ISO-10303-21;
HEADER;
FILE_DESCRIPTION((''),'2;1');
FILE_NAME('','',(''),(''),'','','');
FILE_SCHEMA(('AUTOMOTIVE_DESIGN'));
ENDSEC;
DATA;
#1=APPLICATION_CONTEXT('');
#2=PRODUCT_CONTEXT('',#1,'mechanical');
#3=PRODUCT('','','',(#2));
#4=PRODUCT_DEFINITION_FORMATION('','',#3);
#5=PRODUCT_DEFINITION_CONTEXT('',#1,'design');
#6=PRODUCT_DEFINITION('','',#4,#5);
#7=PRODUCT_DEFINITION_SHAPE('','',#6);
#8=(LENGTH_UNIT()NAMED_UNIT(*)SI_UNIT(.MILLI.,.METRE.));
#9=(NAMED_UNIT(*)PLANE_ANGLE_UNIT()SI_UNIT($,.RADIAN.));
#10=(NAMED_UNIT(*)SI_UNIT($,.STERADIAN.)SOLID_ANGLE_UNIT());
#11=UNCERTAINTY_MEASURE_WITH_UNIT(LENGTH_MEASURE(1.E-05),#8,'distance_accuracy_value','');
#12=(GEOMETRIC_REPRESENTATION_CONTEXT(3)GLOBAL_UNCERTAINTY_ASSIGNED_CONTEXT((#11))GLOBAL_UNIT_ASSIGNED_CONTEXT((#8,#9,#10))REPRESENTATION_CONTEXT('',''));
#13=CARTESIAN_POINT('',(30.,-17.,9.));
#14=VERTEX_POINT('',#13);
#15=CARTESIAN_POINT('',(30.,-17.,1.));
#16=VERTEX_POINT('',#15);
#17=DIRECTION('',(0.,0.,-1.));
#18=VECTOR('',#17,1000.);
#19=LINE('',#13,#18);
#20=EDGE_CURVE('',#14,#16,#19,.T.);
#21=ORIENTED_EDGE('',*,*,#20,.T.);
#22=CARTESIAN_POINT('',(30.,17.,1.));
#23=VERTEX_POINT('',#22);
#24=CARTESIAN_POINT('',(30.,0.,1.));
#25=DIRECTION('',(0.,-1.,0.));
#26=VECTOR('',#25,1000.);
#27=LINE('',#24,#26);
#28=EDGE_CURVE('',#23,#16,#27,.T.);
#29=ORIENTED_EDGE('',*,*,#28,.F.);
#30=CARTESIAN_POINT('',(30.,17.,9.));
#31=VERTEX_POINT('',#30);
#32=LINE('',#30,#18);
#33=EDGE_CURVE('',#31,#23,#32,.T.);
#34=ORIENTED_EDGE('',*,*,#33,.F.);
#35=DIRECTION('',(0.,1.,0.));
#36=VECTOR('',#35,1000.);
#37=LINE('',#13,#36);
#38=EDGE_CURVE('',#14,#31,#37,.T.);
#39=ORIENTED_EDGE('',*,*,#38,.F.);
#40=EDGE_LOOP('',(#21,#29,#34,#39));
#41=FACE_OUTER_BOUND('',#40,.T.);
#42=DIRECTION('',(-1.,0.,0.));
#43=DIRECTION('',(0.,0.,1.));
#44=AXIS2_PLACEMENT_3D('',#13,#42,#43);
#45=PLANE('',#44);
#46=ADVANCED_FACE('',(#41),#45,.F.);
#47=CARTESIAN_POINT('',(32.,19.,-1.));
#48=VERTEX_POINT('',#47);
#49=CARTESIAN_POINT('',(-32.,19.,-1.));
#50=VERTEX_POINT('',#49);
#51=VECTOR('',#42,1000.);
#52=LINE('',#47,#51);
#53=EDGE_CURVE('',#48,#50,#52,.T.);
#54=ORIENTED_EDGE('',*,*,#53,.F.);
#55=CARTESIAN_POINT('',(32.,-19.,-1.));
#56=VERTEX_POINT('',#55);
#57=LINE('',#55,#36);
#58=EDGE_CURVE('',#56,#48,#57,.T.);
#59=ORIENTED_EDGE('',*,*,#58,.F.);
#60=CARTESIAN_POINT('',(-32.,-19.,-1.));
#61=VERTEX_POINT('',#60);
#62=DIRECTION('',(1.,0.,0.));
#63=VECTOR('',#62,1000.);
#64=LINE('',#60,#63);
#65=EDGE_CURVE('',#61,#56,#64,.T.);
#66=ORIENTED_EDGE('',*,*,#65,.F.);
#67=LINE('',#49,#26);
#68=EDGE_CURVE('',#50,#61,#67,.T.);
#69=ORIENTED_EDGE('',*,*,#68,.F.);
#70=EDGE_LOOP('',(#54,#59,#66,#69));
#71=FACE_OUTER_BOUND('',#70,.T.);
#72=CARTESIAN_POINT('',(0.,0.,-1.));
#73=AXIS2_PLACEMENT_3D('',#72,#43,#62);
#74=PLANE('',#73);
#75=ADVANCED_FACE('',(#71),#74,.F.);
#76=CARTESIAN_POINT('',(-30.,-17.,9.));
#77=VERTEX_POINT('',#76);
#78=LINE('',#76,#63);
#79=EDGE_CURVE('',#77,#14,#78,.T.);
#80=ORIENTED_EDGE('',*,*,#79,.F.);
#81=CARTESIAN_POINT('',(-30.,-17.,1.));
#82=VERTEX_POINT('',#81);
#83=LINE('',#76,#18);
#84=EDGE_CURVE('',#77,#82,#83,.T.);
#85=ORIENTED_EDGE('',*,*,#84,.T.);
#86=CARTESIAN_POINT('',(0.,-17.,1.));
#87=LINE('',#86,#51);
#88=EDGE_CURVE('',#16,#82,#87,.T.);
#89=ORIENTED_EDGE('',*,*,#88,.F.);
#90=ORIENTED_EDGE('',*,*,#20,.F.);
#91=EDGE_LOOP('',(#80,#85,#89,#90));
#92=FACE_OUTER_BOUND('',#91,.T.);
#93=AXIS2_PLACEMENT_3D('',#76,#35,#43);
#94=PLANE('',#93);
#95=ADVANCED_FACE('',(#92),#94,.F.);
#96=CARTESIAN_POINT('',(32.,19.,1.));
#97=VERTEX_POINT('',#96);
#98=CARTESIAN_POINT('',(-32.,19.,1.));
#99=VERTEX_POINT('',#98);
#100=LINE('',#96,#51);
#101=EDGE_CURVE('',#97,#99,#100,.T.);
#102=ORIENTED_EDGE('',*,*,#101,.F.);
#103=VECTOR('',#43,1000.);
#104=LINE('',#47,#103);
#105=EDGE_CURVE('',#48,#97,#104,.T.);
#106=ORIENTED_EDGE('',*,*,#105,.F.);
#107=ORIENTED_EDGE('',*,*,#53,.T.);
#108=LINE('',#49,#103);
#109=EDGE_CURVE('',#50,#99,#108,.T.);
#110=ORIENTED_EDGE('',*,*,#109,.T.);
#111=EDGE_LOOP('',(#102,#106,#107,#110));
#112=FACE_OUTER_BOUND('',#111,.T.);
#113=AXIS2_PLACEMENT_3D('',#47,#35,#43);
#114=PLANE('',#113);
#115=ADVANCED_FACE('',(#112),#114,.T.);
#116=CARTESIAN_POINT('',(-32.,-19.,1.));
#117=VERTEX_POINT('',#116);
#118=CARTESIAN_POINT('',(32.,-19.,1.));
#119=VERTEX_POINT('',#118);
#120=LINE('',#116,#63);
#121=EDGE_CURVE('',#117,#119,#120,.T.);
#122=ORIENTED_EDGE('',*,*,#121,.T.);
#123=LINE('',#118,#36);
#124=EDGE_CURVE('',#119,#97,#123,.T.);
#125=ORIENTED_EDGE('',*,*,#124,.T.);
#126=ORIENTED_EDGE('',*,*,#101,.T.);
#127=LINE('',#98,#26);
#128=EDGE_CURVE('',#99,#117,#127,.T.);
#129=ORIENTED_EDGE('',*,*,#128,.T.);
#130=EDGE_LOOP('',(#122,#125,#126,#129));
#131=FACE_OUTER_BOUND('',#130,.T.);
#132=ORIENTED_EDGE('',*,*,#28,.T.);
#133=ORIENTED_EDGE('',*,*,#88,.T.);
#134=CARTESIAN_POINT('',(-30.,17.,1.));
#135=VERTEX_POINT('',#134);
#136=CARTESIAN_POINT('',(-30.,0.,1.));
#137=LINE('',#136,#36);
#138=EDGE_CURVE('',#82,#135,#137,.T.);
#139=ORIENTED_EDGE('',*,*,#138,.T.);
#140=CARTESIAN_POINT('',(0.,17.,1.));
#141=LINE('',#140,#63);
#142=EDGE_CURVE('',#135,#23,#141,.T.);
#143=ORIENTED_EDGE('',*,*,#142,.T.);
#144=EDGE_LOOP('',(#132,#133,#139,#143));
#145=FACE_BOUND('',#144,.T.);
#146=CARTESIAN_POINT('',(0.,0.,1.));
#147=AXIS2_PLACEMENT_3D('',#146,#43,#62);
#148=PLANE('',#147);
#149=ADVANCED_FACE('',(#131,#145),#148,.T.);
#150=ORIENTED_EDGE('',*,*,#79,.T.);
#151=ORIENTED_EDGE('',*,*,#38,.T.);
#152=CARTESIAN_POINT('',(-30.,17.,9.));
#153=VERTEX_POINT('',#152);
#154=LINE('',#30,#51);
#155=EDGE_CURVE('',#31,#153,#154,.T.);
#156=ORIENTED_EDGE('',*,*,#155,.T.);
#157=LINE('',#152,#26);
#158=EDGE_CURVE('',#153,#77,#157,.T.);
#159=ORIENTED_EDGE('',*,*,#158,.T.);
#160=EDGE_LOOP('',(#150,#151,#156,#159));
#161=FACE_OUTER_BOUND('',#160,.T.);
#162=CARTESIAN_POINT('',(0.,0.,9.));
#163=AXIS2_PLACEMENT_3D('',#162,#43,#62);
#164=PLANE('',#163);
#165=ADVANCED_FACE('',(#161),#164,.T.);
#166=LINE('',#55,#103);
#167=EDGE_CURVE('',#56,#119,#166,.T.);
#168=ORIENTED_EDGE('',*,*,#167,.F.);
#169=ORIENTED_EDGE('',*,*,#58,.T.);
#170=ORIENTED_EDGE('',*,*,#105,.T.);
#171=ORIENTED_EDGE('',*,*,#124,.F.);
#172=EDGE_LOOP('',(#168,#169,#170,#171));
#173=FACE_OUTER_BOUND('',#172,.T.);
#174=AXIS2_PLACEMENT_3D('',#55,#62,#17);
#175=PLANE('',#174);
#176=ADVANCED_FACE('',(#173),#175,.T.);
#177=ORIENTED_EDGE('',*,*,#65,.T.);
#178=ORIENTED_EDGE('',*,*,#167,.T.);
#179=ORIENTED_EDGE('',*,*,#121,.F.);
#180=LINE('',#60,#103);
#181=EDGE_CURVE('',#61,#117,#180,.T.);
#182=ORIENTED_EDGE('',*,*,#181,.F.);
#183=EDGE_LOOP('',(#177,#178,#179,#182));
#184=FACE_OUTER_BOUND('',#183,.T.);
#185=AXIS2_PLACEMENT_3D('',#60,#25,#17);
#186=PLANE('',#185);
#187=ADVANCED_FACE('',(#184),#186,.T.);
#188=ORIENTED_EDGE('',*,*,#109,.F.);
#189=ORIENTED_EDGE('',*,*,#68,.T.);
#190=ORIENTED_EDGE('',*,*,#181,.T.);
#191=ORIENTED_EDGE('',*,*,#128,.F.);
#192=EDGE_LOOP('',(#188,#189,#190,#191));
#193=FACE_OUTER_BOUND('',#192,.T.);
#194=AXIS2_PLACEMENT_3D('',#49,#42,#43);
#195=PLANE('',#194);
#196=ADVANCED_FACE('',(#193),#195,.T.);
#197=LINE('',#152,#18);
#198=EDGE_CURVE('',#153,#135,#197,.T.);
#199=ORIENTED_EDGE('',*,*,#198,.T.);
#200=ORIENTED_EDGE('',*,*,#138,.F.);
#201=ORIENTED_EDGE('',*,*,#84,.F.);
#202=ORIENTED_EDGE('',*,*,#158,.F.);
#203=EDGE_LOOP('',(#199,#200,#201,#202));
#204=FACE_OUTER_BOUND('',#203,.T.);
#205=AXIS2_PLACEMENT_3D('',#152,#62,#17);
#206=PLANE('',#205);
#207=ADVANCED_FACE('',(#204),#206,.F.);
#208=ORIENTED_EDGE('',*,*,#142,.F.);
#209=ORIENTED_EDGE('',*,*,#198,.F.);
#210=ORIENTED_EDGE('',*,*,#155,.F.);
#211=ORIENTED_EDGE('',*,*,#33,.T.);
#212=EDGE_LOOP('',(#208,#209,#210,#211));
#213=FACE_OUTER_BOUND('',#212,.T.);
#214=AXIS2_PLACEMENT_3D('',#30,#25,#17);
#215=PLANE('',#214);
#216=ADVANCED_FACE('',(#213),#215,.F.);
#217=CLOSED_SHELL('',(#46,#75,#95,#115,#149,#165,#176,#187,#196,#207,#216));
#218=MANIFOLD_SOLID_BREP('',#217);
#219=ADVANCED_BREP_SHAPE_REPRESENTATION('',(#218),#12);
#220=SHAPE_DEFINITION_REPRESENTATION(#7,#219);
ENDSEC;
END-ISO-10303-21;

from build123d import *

# Parameters (mm, degrees)
SKETCH_1_W      = 64
SKETCH_1_H      = 38
EXTRUDE_1_DEPTH = 1
SKETCH_2_W      = 60
SKETCH_2_H      = 34
EXTRUDE_2_DEPTH = 9


with BuildPart() as part:
    # 草图1 → 凸台-拉伸1 (new, symmetric)
    with BuildSketch(Plane.XY):
        Rectangle(SKETCH_1_W, SKETCH_1_H)
    extrude(amount=EXTRUDE_1_DEPTH, both=True)

    # 草图2 → 凸台-拉伸2 (add)
    with BuildSketch(Plane.XY):
        Rectangle(SKETCH_2_W, SKETCH_2_H)
    extrude(amount=EXTRUDE_2_DEPTH)


solid = part.part
